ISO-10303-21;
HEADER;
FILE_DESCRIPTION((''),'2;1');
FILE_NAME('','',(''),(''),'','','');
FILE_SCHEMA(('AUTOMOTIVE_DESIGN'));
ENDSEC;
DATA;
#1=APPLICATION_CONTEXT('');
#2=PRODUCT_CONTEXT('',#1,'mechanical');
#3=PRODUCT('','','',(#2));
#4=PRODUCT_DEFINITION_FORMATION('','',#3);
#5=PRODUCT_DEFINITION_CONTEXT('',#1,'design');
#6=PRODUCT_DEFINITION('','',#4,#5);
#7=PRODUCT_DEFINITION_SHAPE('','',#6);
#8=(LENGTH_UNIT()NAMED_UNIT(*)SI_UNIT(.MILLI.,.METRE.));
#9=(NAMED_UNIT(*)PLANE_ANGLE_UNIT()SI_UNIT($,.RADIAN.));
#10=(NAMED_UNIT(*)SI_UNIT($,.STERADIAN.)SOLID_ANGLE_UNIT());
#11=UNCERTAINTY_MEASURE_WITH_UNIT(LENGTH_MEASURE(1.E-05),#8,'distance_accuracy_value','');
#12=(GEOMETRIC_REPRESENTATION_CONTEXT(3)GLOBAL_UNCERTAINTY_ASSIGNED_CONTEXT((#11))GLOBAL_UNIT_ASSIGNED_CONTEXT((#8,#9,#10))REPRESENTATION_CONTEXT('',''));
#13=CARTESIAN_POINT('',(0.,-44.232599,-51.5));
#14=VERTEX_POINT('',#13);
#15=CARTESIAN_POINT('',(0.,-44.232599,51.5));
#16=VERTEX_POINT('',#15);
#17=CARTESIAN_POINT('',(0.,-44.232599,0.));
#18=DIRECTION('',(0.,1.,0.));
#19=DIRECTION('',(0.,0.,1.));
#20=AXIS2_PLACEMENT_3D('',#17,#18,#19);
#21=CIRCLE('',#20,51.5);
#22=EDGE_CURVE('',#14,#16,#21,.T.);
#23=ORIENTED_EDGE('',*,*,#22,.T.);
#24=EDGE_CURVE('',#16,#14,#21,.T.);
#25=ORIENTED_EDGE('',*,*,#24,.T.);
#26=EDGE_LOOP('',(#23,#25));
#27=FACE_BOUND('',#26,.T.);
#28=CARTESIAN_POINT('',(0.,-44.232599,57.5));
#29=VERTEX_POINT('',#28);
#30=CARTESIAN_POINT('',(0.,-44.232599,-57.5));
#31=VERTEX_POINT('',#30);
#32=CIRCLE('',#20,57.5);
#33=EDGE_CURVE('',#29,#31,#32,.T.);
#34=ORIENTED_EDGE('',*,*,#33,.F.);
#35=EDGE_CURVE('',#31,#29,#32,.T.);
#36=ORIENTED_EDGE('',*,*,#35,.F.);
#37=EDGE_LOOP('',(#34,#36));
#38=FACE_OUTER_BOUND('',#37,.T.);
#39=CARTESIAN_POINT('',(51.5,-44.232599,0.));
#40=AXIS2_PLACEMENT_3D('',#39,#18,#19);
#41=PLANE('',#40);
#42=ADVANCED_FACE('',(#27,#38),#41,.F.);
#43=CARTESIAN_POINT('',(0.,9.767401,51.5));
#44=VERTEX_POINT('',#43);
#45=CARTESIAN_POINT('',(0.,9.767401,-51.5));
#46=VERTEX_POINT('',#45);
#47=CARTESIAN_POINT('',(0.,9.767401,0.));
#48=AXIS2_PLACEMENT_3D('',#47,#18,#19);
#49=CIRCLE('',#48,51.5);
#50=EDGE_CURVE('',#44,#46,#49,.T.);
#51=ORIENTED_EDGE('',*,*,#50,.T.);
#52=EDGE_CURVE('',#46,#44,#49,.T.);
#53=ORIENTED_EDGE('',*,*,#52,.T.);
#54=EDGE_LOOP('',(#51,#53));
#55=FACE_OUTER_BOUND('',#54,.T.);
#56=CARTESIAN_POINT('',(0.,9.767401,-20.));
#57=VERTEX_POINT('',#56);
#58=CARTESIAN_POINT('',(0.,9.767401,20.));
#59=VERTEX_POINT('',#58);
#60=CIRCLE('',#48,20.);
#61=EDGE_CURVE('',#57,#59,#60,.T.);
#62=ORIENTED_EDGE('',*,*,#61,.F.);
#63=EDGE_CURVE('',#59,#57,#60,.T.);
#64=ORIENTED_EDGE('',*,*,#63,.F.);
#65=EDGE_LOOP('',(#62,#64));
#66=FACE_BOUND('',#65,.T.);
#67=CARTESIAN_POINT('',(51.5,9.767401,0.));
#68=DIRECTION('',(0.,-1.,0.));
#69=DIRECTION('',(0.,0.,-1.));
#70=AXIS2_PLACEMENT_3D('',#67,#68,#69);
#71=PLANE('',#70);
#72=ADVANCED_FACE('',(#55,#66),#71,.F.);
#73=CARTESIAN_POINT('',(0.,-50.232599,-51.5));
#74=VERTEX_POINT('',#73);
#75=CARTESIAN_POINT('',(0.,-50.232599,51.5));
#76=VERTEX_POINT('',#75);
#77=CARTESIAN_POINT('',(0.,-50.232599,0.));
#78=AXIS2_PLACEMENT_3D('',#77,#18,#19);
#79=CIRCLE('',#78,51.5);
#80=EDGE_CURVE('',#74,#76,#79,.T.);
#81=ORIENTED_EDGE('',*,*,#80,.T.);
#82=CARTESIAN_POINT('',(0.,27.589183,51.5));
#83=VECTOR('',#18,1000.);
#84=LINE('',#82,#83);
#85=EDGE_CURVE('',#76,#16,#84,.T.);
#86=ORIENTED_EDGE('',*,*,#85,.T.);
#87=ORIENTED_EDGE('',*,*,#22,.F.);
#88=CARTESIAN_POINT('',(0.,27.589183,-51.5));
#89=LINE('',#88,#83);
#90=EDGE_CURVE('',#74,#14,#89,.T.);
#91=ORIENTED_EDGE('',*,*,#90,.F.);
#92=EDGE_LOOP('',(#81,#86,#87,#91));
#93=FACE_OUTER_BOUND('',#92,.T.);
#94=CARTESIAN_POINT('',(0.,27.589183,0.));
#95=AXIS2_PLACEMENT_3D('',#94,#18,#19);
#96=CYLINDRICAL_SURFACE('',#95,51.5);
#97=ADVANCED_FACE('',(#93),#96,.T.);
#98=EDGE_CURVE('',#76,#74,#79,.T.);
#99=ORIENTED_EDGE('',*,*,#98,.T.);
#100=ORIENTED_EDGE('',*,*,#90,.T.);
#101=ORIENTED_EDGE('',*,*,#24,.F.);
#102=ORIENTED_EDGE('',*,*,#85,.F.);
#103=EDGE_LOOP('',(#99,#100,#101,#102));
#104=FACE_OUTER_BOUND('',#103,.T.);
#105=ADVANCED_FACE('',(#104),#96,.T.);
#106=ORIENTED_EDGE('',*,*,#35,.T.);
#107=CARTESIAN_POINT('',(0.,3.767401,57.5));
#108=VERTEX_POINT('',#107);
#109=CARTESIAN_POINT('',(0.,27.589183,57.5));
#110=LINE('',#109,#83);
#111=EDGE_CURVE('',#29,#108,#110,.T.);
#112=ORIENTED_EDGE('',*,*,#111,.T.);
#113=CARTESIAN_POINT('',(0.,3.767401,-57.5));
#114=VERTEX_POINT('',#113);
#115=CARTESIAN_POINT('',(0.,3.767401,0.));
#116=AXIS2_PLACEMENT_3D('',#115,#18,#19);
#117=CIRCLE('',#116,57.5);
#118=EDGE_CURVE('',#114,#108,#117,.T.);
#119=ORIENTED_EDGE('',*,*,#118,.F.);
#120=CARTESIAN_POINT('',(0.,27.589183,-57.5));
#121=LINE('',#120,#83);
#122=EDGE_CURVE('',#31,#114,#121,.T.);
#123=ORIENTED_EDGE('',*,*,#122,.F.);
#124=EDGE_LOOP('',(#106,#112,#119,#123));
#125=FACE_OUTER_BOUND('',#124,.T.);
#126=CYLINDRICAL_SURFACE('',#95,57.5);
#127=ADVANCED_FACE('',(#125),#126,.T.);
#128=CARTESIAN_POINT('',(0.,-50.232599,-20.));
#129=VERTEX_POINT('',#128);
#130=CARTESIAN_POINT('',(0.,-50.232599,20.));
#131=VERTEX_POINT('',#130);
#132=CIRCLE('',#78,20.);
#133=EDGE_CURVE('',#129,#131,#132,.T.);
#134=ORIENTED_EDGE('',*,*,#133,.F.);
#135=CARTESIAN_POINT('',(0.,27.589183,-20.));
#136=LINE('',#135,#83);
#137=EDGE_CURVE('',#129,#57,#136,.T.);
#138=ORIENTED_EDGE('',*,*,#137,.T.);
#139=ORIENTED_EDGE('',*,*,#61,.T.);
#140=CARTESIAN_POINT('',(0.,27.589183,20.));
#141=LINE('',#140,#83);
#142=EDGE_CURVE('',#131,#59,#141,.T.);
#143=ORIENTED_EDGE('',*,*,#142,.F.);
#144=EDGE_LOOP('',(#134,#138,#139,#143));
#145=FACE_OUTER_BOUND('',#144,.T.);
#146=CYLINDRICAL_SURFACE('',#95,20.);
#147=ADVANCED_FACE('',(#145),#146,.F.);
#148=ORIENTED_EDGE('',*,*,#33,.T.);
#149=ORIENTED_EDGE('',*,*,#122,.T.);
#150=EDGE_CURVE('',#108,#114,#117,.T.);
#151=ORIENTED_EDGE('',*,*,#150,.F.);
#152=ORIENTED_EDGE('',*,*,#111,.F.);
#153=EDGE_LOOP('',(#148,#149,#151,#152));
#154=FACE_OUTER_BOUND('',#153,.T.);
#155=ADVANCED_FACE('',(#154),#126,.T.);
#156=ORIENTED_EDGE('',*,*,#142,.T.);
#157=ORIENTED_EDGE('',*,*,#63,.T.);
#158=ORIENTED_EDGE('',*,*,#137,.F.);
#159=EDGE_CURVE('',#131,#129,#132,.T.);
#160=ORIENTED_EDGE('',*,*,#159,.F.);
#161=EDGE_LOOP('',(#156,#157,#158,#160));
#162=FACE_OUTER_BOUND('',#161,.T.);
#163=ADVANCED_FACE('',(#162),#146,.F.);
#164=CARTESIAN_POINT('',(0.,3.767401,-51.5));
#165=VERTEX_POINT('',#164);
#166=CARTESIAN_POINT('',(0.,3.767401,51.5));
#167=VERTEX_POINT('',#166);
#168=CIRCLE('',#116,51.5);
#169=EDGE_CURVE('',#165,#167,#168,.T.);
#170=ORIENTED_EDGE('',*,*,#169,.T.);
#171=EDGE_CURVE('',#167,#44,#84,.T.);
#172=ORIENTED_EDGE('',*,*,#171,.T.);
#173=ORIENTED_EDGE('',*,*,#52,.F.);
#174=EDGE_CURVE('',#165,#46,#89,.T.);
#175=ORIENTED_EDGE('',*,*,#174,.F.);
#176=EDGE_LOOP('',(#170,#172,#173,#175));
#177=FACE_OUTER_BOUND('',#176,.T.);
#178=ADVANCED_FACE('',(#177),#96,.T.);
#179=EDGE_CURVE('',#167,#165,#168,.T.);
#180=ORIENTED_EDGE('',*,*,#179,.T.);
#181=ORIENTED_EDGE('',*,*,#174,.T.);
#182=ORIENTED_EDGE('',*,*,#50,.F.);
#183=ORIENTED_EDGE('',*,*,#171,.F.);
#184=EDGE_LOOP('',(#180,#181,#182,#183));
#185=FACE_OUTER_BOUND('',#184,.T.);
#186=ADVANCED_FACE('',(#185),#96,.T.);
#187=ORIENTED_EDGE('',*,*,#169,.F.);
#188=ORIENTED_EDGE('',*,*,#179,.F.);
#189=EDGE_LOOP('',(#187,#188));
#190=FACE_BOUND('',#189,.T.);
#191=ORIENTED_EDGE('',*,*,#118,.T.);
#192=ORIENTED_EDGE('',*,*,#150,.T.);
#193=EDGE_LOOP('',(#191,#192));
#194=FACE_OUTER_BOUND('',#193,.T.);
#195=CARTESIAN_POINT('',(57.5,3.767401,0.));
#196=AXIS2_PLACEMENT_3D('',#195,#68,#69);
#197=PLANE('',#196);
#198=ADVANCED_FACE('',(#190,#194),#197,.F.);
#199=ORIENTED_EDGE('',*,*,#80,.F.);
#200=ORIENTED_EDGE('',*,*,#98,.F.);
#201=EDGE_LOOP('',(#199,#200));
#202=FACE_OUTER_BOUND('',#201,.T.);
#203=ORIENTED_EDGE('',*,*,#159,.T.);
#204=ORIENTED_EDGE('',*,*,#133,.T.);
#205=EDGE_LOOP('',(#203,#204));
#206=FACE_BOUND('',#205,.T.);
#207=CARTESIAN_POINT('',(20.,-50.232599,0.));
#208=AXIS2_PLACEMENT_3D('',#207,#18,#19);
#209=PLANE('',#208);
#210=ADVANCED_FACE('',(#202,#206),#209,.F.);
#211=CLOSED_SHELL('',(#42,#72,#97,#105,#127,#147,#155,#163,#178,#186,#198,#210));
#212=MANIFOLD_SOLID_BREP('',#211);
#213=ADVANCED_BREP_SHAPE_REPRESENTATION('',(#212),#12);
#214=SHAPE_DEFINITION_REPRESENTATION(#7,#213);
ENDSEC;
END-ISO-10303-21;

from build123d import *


with BuildPart() as part:
    # 草图1 → 旋转1 (revolve)
    with BuildSketch(Plane.XY, mode=Mode.PRIVATE) as revolve_1_sk:
        Polygon((20, 9.76740105), (20, -50.23259895), (51.5, -50.23259895), (51.5, -44.23259895), (57.5, -44.23259895), (57.5, 3.76740105), (51.5, 3.76740105), (51.5, 9.76740105), align=None)
    revolve(revolve_1_sk.sketch.rotate(Axis((0, 27.589183228, 0), (0, -1, 0)), 90), axis=Axis((0, 27.589183228, 0), (0, -1, 0)))


solid = part.part
